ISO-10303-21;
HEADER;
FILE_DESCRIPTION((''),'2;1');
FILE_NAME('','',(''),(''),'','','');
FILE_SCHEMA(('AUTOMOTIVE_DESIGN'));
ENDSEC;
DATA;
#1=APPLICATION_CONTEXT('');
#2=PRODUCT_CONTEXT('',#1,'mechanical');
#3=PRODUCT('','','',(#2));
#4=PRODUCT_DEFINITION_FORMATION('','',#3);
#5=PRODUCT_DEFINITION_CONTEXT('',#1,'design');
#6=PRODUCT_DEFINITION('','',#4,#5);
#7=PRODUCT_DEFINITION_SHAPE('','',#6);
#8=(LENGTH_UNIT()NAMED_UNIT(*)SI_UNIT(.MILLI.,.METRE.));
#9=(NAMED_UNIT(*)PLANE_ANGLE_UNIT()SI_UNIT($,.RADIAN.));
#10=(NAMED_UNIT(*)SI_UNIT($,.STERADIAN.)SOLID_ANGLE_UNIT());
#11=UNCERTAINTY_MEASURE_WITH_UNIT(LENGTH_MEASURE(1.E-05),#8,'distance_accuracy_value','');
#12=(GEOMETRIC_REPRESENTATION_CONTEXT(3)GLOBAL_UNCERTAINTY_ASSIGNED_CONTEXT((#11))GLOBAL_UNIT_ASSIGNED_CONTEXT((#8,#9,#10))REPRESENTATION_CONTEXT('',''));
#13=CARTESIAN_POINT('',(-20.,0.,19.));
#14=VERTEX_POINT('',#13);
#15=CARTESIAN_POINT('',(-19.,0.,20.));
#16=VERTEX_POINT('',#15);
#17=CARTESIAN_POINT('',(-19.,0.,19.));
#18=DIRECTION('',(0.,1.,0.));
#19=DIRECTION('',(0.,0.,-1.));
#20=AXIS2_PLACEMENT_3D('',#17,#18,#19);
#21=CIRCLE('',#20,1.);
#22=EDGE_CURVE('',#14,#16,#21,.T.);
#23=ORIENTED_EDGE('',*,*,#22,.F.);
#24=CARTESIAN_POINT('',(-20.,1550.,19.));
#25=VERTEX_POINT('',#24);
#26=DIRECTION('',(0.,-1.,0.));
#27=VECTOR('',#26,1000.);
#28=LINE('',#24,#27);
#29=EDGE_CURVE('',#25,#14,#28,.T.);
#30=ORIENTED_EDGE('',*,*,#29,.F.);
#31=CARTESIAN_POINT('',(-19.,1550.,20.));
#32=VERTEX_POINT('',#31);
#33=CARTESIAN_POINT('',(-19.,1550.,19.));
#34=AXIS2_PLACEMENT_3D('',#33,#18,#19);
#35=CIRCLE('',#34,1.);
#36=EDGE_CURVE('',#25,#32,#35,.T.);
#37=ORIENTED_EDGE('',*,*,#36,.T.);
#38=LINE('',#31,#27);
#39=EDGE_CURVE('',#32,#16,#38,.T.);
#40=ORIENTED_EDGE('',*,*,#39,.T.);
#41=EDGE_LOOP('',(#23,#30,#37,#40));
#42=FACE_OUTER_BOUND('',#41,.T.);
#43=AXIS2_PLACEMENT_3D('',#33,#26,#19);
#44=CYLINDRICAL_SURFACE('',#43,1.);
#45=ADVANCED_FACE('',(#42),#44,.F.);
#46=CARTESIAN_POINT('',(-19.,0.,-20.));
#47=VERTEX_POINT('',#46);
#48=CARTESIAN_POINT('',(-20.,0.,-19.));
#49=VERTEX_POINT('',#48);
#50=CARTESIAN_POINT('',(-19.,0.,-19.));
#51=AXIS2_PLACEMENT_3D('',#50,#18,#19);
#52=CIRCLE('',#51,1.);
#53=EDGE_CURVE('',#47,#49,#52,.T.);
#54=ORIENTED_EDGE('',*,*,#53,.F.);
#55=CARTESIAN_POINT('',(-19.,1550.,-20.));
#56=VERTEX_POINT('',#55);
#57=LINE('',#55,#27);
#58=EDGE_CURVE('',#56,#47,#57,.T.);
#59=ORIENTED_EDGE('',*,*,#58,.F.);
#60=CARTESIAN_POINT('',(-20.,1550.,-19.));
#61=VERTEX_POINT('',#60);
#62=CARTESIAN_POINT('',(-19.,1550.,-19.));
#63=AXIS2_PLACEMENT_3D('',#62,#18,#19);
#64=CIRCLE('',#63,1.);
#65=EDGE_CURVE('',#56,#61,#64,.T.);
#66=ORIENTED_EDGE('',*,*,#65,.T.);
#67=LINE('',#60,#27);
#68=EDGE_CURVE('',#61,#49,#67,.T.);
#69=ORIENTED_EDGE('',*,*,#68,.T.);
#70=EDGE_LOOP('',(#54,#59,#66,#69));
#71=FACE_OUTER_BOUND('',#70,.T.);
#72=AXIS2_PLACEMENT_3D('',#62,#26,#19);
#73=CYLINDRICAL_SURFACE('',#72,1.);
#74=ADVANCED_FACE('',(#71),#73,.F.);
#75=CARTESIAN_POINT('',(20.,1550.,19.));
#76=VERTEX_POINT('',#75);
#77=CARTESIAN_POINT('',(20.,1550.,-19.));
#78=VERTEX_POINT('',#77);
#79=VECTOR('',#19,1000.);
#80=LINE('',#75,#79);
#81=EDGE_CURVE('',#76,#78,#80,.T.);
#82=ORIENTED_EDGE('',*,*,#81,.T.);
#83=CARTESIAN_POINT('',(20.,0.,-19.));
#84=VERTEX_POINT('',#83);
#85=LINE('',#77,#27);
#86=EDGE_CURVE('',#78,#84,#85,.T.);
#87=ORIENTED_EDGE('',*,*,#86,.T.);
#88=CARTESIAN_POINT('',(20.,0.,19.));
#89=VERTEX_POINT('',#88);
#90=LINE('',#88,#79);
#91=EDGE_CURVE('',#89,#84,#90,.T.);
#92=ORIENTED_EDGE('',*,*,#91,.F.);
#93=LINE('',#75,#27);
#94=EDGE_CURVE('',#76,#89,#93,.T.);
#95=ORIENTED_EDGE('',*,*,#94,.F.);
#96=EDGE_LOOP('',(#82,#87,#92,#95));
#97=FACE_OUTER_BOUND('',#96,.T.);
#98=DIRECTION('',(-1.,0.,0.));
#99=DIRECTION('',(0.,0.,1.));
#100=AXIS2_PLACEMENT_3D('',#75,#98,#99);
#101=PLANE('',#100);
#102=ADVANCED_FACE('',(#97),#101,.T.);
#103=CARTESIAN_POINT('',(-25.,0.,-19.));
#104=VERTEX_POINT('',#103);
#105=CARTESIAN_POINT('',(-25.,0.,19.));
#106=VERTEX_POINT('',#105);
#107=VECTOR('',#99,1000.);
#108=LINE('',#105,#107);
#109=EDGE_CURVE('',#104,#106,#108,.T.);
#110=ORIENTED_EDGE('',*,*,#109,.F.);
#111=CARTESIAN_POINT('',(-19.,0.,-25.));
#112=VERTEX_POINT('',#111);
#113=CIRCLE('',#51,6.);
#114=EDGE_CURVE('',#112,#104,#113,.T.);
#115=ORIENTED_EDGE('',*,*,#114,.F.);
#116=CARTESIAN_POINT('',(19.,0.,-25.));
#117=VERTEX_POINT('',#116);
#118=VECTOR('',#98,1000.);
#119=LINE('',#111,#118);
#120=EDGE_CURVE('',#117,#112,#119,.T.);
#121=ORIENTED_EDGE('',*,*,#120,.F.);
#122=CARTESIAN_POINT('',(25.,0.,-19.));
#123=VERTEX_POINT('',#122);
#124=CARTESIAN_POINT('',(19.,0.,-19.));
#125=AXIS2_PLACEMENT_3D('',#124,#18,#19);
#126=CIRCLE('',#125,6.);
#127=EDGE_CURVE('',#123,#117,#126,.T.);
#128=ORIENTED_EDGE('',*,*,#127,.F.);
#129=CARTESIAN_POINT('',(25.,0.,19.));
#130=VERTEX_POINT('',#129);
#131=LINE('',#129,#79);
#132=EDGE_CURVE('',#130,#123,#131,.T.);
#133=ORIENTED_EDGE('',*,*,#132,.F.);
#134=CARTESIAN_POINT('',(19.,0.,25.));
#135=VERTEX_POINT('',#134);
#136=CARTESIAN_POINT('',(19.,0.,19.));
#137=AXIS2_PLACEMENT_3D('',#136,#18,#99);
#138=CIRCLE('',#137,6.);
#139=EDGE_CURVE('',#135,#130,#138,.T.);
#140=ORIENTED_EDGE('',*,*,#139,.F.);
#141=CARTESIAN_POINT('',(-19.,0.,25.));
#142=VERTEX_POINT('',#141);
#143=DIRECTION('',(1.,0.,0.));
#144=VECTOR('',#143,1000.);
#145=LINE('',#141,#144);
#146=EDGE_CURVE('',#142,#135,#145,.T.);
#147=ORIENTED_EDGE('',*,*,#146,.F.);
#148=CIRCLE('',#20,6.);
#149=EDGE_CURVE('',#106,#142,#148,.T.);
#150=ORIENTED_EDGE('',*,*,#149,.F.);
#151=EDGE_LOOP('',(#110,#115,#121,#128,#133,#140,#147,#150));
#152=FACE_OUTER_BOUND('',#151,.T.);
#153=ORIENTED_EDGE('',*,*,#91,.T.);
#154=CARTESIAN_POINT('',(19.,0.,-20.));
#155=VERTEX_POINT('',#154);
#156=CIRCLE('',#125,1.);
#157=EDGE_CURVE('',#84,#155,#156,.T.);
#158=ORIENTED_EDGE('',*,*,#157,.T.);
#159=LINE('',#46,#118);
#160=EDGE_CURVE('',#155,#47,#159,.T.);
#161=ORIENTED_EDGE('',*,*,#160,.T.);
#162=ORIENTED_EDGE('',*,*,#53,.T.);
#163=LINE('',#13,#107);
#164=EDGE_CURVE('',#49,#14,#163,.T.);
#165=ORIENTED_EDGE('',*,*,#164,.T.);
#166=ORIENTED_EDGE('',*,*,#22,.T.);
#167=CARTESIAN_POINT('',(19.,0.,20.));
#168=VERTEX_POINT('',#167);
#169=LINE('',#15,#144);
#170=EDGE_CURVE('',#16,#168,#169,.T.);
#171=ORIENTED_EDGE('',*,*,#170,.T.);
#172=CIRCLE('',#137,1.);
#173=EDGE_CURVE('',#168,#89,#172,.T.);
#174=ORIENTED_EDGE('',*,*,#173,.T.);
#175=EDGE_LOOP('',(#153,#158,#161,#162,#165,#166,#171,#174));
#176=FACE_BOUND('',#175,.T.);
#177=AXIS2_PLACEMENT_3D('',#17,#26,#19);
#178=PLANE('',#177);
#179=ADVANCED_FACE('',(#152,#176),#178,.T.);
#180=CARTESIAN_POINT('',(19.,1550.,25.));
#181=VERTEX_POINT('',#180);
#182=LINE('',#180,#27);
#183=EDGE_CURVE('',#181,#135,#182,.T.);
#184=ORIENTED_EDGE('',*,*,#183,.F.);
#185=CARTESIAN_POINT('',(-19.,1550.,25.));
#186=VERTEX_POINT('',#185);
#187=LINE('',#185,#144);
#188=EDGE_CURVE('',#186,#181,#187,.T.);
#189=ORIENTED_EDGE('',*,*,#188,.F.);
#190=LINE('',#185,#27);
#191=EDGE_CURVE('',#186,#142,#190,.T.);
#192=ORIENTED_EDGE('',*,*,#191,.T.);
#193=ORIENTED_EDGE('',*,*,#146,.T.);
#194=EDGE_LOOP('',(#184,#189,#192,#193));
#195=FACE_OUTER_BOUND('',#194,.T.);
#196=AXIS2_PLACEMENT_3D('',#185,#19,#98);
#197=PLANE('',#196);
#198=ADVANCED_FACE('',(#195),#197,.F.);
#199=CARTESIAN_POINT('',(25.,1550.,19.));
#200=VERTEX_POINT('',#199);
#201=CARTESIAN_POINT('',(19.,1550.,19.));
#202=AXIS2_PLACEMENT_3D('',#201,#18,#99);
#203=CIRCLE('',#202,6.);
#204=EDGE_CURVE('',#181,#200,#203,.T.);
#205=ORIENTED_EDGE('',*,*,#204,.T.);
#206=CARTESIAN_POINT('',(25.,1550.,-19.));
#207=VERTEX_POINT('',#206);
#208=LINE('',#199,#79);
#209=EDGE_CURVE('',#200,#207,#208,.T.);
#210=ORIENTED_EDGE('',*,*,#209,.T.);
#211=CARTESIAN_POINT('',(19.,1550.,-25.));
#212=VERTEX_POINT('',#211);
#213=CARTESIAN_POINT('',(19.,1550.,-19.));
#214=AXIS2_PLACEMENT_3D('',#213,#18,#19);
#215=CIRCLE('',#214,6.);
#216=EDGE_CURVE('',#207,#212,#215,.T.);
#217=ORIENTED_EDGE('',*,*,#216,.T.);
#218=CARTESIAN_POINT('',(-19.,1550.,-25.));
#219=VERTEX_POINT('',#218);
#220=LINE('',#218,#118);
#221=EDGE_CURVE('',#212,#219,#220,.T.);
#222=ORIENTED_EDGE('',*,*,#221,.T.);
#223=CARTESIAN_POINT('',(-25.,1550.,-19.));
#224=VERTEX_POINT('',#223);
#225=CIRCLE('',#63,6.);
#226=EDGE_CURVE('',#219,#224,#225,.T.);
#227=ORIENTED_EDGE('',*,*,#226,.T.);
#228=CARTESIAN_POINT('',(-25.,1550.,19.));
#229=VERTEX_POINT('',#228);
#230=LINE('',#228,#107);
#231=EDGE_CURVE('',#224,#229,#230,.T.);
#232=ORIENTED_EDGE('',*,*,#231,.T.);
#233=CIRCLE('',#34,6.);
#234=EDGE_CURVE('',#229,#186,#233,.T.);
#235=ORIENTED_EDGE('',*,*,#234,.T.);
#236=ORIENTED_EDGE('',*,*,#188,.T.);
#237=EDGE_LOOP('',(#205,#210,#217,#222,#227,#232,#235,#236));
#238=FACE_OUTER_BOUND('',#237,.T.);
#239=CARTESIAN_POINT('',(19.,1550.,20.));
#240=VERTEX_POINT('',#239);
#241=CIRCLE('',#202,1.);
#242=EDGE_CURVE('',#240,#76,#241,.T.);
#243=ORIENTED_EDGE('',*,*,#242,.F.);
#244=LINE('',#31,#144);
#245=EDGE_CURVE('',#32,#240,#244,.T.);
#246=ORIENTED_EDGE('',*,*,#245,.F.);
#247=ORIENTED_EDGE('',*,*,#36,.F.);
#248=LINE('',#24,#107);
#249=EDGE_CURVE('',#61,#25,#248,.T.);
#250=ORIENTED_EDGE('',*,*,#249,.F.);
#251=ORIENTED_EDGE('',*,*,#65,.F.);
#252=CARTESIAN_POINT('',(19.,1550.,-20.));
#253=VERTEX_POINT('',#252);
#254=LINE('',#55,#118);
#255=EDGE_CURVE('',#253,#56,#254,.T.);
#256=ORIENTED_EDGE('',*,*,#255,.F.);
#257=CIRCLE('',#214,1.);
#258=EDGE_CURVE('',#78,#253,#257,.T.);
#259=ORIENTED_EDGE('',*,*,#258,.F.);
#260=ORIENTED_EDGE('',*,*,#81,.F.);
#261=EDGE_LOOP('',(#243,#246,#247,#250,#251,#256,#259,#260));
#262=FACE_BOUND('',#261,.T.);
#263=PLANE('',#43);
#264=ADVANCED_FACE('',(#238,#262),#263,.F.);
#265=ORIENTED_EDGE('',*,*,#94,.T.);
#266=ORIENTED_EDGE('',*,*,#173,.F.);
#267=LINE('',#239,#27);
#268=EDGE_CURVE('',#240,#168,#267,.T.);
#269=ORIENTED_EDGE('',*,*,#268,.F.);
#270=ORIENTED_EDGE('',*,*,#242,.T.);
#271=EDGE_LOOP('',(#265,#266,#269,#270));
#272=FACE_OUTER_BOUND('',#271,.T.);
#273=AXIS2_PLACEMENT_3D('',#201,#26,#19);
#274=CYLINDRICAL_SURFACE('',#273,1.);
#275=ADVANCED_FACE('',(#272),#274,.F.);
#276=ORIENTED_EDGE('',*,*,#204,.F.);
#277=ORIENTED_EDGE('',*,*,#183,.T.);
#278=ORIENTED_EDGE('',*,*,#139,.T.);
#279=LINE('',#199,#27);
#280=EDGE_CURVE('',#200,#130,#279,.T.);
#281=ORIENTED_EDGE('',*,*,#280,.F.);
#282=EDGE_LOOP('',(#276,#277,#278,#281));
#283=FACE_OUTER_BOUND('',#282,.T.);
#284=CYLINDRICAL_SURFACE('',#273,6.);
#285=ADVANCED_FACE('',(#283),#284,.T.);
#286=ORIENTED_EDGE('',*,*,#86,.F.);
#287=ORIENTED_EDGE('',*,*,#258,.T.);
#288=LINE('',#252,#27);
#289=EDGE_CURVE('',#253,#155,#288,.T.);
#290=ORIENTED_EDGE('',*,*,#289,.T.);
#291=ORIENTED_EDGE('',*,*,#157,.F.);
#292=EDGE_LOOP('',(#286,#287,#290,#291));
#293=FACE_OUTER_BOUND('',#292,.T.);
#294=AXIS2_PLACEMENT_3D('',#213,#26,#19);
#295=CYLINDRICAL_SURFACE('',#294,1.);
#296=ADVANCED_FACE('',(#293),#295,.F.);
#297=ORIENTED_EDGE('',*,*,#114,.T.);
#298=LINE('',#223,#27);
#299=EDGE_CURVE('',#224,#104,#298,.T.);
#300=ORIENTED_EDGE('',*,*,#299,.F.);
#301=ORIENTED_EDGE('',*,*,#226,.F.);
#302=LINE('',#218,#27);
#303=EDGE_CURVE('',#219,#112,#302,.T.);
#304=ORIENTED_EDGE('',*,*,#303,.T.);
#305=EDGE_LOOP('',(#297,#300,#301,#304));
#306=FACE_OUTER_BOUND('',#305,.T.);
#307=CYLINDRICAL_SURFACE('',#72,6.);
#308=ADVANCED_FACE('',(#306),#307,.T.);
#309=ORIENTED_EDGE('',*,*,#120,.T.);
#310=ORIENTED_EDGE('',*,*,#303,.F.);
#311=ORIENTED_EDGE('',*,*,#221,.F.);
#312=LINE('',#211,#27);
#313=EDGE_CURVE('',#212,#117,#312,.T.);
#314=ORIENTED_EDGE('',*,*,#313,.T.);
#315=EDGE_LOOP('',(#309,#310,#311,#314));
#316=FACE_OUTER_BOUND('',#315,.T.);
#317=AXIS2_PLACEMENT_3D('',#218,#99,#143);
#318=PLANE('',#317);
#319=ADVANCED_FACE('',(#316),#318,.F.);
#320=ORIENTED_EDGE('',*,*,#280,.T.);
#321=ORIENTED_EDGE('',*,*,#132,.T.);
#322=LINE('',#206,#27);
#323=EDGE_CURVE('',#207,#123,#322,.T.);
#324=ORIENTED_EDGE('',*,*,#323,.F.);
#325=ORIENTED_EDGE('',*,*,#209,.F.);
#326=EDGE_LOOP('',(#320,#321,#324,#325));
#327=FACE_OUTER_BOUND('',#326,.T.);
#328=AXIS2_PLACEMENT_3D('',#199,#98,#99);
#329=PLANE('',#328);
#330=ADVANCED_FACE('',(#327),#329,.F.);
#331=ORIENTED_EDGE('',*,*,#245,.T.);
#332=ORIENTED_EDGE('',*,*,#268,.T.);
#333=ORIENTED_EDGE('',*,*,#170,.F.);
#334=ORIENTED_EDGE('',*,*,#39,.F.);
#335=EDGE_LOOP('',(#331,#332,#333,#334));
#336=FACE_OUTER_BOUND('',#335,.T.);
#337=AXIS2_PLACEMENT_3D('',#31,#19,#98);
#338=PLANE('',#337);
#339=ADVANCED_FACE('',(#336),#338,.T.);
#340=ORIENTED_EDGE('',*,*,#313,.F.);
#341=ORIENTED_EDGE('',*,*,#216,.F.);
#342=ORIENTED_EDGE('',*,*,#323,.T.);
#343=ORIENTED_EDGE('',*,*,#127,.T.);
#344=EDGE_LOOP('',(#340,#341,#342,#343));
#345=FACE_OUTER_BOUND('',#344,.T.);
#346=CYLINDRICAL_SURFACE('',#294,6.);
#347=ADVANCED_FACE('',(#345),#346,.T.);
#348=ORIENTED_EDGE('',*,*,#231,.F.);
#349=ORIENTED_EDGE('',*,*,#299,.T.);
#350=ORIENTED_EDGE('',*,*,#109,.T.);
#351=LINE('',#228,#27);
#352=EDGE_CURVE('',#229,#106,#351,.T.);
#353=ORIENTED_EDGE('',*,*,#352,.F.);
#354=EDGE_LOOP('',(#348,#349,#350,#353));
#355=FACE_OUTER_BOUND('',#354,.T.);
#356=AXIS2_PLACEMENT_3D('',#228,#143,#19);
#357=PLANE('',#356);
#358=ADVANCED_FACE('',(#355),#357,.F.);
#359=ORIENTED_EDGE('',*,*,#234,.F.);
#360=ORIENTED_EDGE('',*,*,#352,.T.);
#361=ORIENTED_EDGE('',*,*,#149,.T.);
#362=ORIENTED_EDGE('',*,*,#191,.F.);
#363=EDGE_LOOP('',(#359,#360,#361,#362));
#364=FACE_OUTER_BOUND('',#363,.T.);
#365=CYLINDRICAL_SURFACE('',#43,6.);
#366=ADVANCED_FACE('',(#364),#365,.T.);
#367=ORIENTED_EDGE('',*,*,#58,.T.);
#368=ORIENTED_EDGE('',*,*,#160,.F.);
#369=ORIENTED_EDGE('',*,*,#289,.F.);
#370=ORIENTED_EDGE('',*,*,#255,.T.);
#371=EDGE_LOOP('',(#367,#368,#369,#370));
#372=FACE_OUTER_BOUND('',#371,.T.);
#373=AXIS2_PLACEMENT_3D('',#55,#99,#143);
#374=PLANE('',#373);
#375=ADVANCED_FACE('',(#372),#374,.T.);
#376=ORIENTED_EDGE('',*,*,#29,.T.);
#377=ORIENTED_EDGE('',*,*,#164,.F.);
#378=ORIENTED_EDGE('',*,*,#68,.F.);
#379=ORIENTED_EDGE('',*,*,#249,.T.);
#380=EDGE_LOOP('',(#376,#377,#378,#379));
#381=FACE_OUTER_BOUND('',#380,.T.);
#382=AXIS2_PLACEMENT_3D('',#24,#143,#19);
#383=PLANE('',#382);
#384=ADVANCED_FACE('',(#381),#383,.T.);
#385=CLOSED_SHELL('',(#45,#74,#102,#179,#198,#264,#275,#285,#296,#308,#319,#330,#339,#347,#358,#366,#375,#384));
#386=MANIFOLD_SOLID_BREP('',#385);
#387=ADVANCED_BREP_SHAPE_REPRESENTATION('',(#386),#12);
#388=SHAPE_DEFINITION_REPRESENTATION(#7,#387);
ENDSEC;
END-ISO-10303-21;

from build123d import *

# Parameters (mm, degrees)
EXTRUDE_1_DEPTH = 1550


with BuildPart() as part:
    # 草图1 → 凸台-拉伸1 (new body)
    with BuildSketch(Plane(origin=(0, 0, 0), x_dir=(1, 0, 0), z_dir=(0, 1, 0))):
        with BuildLine():
            Line((-19, -25), (19, -25))
            ThreePointArc((19, -25), (23.242640687, -23.242640687), (25, -19))
            Line((25, -19), (25, 19))
            ThreePointArc((25, 19), (23.242640687, 23.242640687), (19, 25))
            Line((19, 25), (-19, 25))
            ThreePointArc((-19, 25), (-23.242640687, 23.242640687), (-25, 19))
            Line((-25, 19), (-25, -19))
            ThreePointArc((-25, -19), (-23.242640687, -23.242640687), (-19, -25))
        make_face()
        with BuildLine():
            Line((-19, -20), (19, -20))
            ThreePointArc((19, -20), (19.707106781, -19.707106781), (20, -19))
            Line((20, -19), (20, 19))
            ThreePointArc((20, 19), (19.707106781, 19.707106781), (19, 20))
            Line((19, 20), (-19, 20))
            ThreePointArc((-19, 20), (-19.707106781, 19.707106781), (-20, 19))
            Line((-20, 19), (-20, -19))
            ThreePointArc((-20, -19), (-19.707106781, -19.707106781), (-19, -20))
        make_face(mode=Mode.SUBTRACT)
    extrude(amount=EXTRUDE_1_DEPTH)


solid = part.part
